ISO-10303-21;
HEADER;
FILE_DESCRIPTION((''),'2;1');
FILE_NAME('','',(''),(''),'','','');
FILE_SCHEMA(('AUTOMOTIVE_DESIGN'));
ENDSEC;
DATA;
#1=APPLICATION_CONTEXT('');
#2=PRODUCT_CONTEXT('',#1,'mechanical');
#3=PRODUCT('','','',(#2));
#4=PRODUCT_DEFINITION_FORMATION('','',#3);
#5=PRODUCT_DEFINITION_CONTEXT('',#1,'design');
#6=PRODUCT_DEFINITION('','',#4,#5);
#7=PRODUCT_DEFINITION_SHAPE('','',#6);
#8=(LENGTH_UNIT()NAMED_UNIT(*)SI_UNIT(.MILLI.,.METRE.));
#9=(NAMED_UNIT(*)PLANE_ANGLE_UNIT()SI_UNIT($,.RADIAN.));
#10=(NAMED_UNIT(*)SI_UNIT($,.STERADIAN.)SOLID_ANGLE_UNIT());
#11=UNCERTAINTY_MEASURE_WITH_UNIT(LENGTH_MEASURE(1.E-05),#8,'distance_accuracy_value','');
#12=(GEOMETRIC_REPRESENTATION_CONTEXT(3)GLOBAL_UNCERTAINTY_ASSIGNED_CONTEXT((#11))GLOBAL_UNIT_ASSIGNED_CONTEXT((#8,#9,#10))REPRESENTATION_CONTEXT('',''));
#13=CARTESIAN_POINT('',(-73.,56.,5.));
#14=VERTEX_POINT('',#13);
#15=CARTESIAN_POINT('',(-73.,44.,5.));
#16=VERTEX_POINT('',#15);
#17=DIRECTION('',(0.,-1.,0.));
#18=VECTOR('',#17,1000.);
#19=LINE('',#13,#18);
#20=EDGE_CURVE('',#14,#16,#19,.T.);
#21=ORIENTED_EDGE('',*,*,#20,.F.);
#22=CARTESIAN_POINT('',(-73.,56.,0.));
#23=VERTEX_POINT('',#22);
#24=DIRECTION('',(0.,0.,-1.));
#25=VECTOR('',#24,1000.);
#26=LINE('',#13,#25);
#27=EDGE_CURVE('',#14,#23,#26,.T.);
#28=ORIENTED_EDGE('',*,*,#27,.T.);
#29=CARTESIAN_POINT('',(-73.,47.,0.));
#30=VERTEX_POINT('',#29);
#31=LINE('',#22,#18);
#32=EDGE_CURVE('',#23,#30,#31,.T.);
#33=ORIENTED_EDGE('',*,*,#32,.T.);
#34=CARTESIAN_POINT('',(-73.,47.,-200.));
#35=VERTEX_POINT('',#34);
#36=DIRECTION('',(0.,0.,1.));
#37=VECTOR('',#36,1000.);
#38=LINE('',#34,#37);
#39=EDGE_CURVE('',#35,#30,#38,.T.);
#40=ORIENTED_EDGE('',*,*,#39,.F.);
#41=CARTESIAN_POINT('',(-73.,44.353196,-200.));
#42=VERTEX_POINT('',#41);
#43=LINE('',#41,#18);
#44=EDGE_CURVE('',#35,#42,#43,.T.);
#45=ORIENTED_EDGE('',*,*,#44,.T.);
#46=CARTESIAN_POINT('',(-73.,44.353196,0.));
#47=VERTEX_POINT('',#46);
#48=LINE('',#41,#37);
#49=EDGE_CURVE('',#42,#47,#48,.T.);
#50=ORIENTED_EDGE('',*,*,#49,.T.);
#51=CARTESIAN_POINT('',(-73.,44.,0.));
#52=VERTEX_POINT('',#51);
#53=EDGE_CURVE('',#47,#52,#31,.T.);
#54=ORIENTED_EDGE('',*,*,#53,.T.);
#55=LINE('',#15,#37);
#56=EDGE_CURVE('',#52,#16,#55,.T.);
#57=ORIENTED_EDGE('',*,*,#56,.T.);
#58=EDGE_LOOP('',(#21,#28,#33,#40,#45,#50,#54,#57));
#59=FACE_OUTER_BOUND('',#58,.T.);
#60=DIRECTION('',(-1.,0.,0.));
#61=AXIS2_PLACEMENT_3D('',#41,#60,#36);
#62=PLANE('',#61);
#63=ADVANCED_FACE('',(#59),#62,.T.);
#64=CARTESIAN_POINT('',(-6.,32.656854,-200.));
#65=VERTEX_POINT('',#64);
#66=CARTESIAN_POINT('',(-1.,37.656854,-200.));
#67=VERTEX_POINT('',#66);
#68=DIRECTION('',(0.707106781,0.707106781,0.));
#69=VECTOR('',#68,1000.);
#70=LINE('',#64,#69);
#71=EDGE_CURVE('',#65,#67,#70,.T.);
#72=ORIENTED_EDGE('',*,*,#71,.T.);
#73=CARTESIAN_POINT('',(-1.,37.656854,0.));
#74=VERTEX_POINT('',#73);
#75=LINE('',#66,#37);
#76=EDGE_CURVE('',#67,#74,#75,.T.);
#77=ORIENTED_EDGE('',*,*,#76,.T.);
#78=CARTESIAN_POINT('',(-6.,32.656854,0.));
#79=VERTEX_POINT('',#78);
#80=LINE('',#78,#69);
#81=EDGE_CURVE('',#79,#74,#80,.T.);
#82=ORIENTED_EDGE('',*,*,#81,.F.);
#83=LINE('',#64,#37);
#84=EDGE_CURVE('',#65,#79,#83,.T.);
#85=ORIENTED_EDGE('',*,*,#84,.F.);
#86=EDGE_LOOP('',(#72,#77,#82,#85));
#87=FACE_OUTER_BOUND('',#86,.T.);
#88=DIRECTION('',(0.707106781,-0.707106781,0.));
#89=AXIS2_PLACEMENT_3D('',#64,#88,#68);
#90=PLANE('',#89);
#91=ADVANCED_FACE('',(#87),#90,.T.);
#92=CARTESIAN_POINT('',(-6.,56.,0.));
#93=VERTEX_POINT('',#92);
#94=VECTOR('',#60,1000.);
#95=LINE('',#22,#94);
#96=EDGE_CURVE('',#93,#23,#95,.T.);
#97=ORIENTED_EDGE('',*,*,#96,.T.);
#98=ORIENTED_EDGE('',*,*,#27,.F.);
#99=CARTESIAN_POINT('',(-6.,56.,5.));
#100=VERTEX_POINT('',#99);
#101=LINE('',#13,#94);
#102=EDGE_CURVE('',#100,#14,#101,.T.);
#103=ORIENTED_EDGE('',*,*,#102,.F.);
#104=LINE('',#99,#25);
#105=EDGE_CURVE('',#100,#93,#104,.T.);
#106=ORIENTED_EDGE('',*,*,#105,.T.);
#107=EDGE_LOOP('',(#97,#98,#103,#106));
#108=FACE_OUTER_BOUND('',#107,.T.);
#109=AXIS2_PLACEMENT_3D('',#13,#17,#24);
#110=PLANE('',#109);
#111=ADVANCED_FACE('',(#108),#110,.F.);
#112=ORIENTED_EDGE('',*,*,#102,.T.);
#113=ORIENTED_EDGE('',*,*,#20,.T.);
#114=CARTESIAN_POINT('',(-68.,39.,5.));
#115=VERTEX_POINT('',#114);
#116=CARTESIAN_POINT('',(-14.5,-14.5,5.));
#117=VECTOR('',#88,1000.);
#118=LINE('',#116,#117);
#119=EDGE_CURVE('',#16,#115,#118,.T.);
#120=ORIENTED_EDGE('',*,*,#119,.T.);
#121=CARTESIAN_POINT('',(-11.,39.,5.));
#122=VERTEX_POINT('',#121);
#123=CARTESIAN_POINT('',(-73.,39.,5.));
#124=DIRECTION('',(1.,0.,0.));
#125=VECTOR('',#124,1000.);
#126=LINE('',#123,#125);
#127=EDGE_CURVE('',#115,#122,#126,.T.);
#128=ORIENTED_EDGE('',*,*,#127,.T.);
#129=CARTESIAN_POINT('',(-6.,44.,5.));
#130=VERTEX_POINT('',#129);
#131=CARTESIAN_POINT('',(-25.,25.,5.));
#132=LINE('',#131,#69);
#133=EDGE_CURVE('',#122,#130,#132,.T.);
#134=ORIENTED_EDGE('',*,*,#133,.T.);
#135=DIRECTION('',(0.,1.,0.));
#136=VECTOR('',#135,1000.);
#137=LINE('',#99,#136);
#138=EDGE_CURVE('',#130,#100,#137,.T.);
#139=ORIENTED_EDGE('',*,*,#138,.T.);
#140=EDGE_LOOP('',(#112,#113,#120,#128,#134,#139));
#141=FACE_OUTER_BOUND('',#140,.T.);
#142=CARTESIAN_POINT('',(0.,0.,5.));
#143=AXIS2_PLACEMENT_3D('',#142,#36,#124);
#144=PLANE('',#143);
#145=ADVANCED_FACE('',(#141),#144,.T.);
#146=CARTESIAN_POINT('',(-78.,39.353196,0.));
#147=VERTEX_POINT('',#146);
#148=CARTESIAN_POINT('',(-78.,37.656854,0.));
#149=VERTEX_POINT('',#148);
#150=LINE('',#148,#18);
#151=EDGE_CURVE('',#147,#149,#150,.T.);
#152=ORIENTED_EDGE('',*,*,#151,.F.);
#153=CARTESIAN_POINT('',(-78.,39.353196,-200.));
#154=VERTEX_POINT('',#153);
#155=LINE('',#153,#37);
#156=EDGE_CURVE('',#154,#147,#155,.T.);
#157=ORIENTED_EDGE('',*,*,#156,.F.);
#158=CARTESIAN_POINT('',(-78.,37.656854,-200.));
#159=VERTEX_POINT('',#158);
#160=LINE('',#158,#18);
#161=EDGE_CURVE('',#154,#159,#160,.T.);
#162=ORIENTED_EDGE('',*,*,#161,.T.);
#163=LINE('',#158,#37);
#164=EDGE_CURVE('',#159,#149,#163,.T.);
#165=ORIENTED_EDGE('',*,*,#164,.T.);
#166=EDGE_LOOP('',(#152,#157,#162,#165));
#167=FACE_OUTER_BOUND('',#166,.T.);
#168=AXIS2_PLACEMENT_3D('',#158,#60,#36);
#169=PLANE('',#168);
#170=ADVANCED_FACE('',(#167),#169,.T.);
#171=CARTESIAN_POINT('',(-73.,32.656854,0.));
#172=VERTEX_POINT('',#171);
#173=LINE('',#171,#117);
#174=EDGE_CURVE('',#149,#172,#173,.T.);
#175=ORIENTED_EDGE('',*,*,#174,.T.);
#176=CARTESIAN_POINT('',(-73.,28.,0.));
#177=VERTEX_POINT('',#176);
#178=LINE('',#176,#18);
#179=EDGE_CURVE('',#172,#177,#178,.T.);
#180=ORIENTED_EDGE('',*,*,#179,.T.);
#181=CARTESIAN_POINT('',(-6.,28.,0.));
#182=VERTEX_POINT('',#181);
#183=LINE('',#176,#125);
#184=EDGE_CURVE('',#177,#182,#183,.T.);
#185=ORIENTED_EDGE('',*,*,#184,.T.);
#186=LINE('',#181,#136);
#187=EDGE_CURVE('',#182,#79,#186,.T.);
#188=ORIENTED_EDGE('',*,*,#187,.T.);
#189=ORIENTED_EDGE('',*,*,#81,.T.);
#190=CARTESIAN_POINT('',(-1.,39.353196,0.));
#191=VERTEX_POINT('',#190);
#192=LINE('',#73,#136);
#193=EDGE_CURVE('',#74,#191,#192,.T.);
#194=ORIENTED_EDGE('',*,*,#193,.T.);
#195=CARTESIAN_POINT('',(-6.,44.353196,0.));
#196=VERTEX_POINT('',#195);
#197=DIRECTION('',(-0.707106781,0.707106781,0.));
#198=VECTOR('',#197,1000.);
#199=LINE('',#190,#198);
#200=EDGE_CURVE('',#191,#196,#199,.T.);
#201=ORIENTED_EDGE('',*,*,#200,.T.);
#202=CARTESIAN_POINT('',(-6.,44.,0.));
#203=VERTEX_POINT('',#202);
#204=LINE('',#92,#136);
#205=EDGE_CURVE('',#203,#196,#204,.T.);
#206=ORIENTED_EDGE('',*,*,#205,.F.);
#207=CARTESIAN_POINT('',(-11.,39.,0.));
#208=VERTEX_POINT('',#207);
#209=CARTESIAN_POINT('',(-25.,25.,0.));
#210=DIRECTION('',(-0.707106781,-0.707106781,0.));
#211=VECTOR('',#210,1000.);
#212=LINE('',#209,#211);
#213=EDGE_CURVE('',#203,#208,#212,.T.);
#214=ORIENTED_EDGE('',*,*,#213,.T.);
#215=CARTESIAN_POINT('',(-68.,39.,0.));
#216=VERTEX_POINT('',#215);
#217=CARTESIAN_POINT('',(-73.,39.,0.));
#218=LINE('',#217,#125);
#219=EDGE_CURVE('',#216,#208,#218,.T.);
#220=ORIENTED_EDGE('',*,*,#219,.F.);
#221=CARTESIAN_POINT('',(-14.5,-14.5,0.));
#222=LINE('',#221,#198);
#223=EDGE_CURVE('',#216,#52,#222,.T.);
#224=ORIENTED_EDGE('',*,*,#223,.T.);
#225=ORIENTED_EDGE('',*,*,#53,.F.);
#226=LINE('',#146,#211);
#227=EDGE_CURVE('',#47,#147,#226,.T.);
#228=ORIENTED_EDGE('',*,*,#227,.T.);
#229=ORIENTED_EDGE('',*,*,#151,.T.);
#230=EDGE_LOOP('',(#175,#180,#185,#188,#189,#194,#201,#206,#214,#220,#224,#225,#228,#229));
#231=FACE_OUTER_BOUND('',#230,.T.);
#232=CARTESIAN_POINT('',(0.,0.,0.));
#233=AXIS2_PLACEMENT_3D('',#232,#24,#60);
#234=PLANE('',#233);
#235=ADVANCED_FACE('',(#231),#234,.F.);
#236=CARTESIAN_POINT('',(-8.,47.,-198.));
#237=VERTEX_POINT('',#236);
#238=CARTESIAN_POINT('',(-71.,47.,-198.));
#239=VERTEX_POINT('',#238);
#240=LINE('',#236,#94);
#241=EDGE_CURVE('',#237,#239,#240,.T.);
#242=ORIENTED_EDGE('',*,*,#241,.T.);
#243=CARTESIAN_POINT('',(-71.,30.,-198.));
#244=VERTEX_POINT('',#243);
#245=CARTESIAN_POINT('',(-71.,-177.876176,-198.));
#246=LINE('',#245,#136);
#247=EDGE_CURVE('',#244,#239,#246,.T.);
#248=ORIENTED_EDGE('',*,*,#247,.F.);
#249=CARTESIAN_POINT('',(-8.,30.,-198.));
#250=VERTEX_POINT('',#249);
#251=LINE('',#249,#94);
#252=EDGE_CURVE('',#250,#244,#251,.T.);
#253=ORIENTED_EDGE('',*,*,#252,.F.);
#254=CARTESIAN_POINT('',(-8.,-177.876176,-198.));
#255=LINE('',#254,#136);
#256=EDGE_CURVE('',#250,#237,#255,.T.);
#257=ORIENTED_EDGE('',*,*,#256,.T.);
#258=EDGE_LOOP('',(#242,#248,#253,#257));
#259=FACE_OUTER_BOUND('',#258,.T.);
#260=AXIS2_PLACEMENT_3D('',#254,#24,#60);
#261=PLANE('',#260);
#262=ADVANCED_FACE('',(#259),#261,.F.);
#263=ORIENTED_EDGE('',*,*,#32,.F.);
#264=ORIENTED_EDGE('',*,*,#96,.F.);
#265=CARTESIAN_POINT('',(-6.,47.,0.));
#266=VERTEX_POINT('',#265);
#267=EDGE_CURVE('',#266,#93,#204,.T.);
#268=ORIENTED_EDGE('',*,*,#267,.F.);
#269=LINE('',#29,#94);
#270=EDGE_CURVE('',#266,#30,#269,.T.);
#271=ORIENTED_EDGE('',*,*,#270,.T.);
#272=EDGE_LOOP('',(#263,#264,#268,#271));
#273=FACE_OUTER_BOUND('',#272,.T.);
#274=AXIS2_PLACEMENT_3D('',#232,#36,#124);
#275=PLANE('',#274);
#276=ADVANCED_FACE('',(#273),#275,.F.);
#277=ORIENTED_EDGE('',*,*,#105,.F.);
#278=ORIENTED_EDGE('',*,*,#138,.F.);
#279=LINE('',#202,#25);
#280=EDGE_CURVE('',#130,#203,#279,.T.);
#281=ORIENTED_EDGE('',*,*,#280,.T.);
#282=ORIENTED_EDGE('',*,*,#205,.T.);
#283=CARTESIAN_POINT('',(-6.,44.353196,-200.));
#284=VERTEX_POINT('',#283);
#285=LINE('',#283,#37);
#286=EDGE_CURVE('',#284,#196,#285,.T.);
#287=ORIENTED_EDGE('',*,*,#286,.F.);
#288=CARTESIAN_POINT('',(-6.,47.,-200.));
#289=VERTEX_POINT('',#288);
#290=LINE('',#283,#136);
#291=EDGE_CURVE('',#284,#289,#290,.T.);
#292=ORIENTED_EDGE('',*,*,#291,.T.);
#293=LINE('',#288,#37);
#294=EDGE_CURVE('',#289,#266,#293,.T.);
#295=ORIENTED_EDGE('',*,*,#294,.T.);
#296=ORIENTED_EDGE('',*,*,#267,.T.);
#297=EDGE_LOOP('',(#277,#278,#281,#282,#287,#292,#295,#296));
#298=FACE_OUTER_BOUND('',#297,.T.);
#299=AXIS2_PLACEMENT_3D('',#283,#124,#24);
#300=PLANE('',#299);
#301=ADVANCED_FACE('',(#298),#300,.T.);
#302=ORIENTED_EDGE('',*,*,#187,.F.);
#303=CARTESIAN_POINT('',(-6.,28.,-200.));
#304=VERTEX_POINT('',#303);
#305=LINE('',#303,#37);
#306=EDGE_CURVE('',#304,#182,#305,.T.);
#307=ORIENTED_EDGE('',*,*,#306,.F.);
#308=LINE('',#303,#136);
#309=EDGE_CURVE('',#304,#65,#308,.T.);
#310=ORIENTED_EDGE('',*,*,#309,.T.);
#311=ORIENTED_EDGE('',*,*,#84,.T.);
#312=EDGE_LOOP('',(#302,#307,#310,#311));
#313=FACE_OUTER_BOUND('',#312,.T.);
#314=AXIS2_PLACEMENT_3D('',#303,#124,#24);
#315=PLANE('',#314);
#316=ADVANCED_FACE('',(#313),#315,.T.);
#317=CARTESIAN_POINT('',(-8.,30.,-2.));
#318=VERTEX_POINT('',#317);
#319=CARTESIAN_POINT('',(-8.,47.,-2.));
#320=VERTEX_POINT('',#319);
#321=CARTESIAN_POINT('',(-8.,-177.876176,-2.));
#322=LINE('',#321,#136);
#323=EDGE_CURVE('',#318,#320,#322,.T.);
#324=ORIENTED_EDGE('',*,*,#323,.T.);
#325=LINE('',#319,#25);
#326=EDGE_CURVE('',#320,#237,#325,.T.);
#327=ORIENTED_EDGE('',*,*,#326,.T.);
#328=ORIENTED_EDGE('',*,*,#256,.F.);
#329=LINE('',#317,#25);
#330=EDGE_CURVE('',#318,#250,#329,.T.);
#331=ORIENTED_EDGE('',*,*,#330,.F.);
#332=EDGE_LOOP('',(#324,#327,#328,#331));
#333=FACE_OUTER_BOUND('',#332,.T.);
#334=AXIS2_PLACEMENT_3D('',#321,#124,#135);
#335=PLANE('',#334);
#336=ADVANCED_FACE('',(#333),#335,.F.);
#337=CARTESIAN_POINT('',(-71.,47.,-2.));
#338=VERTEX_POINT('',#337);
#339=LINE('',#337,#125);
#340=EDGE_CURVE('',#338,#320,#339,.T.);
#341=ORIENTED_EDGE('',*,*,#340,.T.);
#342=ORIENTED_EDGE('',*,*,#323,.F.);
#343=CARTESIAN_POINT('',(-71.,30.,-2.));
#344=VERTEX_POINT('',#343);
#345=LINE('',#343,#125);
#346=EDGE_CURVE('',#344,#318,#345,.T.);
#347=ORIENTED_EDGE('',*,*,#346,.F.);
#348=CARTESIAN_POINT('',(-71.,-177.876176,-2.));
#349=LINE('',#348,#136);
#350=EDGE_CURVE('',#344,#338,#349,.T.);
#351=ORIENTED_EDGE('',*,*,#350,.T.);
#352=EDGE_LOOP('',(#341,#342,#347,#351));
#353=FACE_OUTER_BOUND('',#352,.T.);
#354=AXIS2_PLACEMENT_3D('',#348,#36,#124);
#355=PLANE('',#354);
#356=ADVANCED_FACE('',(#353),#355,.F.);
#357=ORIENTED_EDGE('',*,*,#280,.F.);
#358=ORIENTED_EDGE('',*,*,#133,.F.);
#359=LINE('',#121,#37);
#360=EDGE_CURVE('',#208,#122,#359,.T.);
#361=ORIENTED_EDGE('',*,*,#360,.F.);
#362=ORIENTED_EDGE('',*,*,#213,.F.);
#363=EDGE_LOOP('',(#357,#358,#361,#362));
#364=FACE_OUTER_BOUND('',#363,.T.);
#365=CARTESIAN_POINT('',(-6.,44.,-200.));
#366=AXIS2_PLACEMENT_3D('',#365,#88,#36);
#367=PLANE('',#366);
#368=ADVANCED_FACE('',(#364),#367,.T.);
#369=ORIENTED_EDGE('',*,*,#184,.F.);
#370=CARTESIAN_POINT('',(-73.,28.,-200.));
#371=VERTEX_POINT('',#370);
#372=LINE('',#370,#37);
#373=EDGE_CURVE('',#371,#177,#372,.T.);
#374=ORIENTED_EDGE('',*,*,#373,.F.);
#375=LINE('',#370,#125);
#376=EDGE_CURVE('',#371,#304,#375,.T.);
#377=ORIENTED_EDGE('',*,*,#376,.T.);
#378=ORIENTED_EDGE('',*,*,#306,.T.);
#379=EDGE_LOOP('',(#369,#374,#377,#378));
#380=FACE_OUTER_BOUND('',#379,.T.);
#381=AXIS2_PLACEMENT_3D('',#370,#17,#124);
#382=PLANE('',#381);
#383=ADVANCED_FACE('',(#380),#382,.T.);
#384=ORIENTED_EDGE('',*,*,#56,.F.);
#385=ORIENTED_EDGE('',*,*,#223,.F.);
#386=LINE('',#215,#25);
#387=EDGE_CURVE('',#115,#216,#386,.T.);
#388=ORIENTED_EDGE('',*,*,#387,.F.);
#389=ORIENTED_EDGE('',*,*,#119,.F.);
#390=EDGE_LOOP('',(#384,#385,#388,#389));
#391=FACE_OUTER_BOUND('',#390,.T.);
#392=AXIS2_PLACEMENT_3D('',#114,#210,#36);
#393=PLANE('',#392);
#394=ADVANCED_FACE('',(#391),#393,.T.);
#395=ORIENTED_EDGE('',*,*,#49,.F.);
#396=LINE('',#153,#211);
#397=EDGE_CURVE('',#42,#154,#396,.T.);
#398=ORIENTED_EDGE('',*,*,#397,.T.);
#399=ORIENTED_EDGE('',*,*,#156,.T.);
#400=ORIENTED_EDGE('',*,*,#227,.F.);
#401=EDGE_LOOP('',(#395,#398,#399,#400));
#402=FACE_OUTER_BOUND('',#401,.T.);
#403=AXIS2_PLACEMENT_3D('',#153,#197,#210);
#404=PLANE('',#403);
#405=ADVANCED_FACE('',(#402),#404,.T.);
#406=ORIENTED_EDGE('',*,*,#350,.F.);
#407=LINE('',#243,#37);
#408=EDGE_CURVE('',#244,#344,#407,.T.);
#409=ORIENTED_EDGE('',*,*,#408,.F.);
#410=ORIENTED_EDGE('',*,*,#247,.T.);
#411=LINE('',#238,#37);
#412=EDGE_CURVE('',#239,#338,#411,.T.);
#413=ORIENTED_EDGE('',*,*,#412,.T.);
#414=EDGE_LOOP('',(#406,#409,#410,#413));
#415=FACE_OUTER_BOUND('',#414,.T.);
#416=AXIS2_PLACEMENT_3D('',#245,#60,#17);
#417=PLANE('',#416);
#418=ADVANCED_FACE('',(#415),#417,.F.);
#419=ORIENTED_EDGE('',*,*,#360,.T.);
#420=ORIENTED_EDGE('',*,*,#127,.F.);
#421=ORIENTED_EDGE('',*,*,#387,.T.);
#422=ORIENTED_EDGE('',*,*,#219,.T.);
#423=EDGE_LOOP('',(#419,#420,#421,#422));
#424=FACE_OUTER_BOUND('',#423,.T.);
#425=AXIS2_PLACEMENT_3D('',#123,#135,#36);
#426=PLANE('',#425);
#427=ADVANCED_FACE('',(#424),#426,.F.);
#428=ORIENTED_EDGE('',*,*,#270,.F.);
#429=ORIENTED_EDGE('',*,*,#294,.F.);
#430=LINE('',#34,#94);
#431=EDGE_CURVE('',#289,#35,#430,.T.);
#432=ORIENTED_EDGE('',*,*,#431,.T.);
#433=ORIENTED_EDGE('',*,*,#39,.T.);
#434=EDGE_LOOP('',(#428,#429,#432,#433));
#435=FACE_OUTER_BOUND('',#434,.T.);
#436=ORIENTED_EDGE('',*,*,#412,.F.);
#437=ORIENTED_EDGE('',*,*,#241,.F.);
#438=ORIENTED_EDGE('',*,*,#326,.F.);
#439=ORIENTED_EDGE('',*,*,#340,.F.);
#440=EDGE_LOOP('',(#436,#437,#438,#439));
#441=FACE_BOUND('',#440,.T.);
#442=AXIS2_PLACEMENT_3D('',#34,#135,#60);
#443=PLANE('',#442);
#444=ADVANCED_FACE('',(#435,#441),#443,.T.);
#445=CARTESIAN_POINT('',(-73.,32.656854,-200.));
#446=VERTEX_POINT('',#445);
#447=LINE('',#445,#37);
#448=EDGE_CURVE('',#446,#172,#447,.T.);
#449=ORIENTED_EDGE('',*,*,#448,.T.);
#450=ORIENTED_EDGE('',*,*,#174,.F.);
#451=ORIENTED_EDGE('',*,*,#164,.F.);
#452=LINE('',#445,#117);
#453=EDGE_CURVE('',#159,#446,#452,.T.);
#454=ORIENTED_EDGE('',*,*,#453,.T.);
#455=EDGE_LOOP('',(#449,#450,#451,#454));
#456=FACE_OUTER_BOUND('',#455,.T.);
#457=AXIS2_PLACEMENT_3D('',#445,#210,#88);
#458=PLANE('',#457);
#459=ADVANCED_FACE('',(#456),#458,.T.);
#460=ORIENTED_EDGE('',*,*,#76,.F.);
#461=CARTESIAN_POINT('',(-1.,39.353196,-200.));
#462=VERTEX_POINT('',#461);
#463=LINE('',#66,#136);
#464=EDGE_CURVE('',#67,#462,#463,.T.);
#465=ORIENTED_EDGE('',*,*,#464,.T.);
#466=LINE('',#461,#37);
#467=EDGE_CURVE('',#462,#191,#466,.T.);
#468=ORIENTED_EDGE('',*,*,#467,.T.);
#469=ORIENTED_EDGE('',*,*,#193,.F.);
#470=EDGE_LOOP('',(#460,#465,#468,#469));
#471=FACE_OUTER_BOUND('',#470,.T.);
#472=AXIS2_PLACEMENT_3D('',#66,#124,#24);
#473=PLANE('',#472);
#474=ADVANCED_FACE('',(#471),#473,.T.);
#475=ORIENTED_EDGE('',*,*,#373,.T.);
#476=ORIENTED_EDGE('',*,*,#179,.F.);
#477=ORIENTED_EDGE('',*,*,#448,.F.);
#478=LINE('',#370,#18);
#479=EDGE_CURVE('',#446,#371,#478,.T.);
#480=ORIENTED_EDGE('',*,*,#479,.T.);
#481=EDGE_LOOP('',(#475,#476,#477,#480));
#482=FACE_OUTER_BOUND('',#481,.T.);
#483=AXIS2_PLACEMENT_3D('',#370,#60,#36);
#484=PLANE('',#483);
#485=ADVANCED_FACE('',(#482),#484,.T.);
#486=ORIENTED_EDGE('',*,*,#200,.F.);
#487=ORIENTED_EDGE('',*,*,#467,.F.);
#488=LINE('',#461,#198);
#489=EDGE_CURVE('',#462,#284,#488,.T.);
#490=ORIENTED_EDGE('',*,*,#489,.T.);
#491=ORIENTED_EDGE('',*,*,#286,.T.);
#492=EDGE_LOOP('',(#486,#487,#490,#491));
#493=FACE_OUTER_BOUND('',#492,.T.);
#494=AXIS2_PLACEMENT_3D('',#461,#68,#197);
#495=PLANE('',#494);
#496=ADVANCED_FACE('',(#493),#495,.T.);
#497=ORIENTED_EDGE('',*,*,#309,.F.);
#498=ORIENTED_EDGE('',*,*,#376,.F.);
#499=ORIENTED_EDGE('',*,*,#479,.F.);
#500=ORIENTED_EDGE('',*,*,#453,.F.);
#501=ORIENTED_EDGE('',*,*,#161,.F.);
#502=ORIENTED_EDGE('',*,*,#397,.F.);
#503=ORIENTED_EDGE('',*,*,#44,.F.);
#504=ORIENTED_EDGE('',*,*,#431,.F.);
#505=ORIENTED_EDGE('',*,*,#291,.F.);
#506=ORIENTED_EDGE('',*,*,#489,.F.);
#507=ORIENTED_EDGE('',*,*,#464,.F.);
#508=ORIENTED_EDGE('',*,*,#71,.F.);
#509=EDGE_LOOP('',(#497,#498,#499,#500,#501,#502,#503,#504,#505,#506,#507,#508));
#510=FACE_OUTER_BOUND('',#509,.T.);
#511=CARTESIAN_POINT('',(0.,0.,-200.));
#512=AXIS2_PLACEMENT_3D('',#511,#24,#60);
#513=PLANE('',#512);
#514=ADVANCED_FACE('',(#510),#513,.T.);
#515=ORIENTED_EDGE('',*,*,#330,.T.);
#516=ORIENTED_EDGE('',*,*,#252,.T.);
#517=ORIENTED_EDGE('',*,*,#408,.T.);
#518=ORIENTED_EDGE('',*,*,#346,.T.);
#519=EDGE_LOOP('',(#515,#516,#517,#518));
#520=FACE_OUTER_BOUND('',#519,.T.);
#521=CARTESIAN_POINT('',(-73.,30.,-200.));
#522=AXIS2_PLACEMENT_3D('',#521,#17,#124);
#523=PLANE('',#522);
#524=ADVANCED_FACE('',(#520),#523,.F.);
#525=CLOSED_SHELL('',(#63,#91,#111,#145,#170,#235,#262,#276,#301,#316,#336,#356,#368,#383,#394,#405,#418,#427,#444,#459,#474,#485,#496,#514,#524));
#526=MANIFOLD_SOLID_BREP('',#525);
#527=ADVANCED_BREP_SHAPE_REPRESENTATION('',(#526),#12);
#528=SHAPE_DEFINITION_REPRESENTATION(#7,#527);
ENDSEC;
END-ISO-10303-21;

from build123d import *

# Parameters (mm, degrees)
BOSS_EXTRUDE1_DEPTH = 200
SKETCH2_W           = 63
SKETCH2_H           = 196
CUT_EXTRUDE1_DEPTH  = 17
SKETCH3_W           = 67
SKETCH3_H           = 17
BOSS_EXTRUDE2_DEPTH = 5
CHAMFER1_SIZE       = 5


with BuildPart() as part:
    # Sketch1 → Boss-Extrude1 (new body)
    with BuildSketch(Plane.XY):
        Polygon((-73, 28), (-6, 28), (-6, 32.656854249), (-1, 37.656854249), (-1, 39.353196257), (-6, 44.353196257), (-6, 47), (-73, 47), (-73, 44.353196257), (-78, 39.353196257), (-78, 37.656854249), (-73, 32.656854249), align=None)
    extrude(amount=-BOSS_EXTRUDE1_DEPTH)

    # Sketch2 → Cut-Extrude1 (cut)
    with BuildSketch(Plane(origin=(0, 47, 0), x_dir=(1, 0, 0), z_dir=(0, 1, 0))):
        with Locations((-39.5, 100)):
            Rectangle(SKETCH2_W, SKETCH2_H)
    extrude(amount=-CUT_EXTRUDE1_DEPTH, mode=Mode.SUBTRACT)

    # Sketch3 → Boss-Extrude2 (add)
    with BuildSketch(Plane.XY):
        with Locations((-39.5, 47.5)):
            Rectangle(SKETCH3_W, SKETCH3_H)
    extrude(amount=BOSS_EXTRUDE2_DEPTH)

    # Chamfer1
    chamfer1_edges = [part.edges().sort_by_distance(p)[0] for p in [
        (-73, 39, 2.5),
        (-6, 39, 2.5),
    ]]
    chamfer(chamfer1_edges, length=CHAMFER1_SIZE)


solid = part.part
